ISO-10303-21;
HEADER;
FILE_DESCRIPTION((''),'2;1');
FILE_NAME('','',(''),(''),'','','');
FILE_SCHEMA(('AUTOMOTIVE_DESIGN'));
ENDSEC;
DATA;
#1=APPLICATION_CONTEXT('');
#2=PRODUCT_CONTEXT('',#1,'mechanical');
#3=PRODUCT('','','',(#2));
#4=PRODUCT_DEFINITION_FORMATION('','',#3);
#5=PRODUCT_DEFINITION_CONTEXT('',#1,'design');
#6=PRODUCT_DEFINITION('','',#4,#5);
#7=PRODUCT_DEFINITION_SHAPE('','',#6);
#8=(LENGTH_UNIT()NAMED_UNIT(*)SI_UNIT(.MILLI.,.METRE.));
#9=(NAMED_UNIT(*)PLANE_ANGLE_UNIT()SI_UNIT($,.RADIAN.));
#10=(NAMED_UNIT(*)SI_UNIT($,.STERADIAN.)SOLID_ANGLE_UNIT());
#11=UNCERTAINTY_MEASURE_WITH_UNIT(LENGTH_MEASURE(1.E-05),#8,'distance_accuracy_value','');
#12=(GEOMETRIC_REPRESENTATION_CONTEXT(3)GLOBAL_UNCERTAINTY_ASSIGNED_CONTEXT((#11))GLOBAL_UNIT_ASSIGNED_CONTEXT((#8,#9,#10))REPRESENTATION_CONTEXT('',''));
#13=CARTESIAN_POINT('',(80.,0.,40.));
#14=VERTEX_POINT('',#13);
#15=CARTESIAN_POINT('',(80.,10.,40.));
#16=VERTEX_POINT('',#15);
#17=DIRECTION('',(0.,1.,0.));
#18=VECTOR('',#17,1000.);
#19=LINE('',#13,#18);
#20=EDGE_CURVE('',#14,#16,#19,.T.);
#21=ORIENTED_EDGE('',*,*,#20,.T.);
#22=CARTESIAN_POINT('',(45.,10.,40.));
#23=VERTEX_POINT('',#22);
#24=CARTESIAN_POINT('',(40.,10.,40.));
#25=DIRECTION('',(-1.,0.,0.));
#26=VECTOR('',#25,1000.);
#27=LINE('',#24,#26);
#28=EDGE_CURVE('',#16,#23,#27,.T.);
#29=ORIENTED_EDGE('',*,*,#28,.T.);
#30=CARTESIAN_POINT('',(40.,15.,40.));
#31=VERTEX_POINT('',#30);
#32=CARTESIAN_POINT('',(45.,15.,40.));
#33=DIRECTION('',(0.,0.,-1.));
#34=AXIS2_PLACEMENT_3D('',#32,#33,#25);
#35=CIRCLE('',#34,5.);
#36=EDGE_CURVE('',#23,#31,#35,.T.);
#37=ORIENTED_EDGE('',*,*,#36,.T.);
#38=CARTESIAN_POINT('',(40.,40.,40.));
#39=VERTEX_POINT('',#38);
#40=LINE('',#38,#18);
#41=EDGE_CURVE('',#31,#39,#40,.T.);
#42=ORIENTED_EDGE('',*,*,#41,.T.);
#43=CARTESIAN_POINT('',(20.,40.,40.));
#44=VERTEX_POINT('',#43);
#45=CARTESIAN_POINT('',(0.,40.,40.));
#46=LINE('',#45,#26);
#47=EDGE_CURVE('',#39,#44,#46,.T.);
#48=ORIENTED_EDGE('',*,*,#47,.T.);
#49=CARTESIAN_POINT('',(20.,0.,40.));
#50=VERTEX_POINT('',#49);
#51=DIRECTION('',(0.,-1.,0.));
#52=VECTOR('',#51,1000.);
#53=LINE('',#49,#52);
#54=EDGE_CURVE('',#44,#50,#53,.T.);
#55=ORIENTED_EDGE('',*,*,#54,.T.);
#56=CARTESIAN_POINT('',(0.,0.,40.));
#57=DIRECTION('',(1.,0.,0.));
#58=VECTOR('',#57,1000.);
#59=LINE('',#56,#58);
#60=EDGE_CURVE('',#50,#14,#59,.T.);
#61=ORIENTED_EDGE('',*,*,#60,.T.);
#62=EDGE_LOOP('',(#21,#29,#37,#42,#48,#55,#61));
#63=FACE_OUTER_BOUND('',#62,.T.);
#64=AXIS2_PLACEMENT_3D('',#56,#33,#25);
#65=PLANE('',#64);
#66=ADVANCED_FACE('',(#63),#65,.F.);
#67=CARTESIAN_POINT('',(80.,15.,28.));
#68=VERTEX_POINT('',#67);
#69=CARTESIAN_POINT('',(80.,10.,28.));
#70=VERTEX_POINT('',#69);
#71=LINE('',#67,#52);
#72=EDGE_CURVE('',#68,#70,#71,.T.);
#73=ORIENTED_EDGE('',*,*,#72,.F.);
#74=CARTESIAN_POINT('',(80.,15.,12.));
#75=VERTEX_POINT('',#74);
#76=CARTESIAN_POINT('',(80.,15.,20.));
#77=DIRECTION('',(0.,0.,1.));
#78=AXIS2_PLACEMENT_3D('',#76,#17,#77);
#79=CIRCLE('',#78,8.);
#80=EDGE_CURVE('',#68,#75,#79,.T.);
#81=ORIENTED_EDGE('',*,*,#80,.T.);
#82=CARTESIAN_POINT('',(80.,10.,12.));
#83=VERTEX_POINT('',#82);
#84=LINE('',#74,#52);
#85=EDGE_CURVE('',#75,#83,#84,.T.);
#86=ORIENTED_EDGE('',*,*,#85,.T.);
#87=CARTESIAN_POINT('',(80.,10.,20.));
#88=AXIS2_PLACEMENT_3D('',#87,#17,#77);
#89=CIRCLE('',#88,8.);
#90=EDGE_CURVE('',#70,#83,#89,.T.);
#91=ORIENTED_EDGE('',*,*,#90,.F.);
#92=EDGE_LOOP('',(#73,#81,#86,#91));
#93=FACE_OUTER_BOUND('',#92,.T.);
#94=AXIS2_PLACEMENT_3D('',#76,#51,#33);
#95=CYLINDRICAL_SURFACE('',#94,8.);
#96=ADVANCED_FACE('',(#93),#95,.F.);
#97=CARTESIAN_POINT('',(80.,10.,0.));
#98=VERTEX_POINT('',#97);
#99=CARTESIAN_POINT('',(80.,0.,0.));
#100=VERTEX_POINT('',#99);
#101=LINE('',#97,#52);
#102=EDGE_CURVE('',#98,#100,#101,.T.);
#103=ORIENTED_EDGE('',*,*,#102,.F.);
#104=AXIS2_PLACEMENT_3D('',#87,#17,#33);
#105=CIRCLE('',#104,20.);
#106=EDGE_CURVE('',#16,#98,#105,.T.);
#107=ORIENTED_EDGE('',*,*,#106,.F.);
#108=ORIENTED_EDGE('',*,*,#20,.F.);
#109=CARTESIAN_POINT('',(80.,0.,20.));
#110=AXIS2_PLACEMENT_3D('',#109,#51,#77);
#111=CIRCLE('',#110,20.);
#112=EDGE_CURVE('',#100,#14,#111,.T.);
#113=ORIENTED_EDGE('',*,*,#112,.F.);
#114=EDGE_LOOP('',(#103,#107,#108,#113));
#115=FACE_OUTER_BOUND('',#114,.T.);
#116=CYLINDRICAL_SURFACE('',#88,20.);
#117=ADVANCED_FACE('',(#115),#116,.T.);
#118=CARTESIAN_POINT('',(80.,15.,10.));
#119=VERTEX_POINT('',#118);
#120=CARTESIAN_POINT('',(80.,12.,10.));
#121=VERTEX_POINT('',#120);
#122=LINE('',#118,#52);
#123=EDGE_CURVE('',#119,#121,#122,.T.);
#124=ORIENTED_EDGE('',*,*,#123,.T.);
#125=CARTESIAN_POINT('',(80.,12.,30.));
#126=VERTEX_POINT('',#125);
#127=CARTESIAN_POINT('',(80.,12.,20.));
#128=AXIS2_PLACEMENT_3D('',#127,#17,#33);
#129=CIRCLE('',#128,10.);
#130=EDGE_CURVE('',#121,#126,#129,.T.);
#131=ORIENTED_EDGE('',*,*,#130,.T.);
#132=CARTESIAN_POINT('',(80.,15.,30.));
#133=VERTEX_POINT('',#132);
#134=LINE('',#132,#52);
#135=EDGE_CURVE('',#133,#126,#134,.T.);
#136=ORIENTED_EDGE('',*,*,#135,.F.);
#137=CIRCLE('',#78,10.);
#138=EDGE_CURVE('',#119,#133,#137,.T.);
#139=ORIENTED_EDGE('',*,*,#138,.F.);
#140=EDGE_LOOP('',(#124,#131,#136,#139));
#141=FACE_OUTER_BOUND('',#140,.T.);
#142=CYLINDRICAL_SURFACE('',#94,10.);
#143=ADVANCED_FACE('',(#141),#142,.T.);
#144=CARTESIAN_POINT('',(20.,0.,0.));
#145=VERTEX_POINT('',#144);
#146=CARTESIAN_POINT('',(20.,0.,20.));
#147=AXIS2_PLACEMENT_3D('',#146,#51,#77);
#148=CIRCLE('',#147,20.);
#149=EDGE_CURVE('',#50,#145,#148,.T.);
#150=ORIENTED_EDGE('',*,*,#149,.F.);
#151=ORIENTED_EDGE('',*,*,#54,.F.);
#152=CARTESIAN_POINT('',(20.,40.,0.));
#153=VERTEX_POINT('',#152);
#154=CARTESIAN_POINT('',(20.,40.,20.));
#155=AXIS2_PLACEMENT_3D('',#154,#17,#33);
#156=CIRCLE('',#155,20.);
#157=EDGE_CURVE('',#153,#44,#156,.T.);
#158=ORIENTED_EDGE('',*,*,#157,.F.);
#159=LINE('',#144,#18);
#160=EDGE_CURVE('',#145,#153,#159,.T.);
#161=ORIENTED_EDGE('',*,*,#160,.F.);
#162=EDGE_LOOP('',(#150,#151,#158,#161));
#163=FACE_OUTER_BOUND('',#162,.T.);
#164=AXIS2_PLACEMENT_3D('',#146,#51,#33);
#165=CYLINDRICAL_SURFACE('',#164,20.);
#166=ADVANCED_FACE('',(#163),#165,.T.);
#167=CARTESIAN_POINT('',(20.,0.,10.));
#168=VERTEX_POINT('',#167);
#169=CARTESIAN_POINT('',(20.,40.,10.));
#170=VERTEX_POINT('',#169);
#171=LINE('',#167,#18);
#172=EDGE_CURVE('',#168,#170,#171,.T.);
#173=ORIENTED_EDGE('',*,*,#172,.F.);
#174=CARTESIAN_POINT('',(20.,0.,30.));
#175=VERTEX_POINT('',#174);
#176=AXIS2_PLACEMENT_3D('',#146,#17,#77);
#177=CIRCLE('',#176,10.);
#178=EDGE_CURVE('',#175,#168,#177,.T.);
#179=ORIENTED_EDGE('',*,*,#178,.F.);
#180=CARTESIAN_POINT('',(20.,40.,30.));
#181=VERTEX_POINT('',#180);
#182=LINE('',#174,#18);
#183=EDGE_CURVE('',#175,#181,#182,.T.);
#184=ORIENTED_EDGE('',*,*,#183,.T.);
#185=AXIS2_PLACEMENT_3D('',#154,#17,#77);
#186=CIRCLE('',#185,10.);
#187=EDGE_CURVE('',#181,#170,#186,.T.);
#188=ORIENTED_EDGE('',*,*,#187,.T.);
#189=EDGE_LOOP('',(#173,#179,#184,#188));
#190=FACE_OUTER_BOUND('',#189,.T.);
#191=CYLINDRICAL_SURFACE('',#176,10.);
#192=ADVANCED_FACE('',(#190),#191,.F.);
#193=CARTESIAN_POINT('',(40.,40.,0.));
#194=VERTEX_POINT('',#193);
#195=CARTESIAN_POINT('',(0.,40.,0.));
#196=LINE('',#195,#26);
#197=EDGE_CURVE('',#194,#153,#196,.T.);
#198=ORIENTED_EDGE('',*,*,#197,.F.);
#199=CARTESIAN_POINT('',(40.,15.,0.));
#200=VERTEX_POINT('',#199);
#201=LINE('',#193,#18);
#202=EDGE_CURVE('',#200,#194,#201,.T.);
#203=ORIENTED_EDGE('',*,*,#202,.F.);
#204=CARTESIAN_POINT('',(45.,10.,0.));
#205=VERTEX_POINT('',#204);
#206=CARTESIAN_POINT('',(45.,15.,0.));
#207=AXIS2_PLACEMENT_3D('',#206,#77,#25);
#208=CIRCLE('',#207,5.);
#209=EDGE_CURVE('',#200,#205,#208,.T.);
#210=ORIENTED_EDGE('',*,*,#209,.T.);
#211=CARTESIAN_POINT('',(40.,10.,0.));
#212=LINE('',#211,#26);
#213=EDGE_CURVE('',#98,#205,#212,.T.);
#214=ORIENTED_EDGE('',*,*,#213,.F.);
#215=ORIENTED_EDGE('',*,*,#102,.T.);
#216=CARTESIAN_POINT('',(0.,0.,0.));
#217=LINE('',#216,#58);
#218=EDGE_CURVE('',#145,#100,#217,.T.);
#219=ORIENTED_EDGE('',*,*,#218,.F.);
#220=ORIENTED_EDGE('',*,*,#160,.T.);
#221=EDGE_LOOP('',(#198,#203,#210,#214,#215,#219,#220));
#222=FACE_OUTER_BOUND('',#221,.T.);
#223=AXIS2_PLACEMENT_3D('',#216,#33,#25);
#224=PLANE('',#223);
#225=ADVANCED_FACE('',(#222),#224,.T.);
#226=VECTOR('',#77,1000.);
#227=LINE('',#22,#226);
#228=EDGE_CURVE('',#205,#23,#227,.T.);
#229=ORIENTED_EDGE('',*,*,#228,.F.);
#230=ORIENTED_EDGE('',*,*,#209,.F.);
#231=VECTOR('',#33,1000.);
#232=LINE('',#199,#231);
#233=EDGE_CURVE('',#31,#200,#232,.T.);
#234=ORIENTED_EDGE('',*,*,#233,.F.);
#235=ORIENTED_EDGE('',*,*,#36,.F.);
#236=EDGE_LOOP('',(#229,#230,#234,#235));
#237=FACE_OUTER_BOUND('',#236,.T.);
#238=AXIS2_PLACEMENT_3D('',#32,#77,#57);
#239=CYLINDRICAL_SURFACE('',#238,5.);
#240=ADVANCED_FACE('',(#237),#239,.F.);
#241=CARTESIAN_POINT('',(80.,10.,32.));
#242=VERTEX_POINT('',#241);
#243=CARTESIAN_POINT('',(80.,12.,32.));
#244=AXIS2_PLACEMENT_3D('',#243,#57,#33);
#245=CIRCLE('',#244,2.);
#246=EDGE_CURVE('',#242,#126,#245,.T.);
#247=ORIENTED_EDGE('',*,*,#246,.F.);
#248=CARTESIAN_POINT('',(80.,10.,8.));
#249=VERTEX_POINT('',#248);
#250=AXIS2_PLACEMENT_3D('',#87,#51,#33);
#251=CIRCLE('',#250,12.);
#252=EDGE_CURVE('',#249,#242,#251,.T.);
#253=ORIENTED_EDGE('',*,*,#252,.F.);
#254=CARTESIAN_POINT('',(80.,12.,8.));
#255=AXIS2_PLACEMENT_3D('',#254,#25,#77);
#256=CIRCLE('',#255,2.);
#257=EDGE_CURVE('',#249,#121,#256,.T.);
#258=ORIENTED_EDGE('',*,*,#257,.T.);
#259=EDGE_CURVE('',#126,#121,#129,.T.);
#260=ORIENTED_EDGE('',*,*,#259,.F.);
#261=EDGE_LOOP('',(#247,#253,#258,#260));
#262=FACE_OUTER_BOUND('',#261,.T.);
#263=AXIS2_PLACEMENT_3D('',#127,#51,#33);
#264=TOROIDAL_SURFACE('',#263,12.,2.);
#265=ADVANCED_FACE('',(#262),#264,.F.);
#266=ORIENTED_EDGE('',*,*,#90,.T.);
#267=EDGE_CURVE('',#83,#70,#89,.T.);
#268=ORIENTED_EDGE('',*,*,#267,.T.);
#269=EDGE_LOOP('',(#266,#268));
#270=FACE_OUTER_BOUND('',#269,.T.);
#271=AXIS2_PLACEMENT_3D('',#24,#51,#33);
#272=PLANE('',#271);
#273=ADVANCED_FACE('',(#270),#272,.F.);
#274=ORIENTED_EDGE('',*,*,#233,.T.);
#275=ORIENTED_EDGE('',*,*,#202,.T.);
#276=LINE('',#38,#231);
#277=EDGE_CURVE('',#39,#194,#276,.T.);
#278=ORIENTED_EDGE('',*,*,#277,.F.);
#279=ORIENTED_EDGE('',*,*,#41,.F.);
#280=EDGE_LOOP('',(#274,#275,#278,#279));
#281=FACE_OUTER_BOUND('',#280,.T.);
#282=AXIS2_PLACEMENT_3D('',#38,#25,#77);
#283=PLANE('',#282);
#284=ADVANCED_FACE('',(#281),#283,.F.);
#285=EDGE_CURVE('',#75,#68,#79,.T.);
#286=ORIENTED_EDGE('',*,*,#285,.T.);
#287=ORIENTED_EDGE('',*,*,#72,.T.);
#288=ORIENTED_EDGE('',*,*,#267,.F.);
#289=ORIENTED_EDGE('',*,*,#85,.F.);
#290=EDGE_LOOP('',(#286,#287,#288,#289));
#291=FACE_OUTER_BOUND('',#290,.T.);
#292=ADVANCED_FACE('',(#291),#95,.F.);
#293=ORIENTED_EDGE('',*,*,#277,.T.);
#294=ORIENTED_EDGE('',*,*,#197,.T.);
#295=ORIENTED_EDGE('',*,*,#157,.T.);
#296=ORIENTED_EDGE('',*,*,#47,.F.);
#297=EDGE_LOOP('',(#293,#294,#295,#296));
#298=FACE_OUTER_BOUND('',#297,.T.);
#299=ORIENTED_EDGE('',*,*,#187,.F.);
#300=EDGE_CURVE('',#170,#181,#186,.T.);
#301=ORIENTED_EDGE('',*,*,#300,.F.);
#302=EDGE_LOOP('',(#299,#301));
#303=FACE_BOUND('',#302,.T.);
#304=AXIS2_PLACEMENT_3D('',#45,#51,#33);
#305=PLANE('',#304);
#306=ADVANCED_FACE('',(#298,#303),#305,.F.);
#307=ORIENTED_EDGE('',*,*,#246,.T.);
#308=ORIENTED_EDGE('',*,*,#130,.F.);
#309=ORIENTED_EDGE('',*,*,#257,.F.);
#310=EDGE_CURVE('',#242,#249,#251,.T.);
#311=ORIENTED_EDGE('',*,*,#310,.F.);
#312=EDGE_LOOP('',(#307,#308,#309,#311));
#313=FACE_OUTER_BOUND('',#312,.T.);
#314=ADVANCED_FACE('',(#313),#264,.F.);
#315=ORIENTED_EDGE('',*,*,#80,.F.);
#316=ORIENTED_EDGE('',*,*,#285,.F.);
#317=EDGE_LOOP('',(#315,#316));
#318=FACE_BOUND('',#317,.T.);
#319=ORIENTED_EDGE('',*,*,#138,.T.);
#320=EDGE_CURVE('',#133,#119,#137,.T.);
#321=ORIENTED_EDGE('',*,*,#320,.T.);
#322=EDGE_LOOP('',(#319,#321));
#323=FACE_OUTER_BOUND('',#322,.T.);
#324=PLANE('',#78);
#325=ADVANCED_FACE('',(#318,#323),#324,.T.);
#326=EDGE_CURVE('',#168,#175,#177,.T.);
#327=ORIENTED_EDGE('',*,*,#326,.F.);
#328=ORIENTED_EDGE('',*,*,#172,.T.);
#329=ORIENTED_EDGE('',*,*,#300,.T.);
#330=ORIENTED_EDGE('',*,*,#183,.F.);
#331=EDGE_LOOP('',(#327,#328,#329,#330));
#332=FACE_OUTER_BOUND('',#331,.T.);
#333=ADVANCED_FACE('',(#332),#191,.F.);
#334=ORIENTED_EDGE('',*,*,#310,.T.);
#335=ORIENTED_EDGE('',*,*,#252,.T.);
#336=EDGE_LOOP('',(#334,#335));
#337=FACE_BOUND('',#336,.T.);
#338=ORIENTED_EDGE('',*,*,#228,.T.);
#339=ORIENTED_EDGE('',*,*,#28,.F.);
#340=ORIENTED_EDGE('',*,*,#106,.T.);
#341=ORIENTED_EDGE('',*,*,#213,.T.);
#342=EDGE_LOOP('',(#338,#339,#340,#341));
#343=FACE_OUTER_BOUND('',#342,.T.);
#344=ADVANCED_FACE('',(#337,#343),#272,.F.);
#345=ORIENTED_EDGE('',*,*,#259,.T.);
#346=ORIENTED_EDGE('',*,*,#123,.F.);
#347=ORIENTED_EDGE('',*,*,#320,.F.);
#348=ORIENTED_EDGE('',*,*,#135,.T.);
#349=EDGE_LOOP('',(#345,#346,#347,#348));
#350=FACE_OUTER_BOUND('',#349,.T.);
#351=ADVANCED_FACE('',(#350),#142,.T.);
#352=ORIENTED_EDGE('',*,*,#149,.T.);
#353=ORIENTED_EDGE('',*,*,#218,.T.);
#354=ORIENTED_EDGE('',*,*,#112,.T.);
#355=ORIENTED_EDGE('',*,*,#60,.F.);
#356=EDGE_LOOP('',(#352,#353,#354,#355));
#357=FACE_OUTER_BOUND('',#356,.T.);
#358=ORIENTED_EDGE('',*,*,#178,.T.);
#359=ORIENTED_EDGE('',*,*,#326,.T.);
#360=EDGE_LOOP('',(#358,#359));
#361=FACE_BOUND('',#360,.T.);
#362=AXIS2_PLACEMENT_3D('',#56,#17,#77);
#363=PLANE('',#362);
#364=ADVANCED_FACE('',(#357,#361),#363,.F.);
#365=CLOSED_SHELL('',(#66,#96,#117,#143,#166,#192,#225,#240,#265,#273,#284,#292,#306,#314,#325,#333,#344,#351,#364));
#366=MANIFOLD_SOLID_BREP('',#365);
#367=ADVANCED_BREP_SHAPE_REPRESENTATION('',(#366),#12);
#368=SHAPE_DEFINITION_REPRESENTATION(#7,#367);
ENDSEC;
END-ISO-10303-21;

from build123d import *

# Parameters (mm, degrees)
L_BODY_DEPTH               = 40
LUG_END_ROUND_RADIUS       = 20
LUG_END_ROUND_LENGTH       = 40
LUG_BORE_SKETCH_R          = 10
LUG_BORE_20_DEPTH          = 40
BASE_END_ROUND_RADIUS      = 20
BASE_END_ROUND_LENGTH      = 10
RING_BOSS_SKETCH_R         = 10
RING_BOSS_SKETCH_R_2       = 8
RING_BOSS_20X_16_DEPTH     = 5
INNER_CORNER_FILLET_R5_R   = 5
RING_BOSS_BASE_FILLET_R2_R = 2


with BuildPart() as part:
    # L Profile Sketch → L Body (new body)
    with BuildSketch(Plane.XY):
        Polygon((0, 0), (100, 0), (100, 10), (40, 10), (40, 40), (0, 40), align=None)
    extrude(amount=L_BODY_DEPTH)

    # Lug End Round: full round fillet: the end face becomes a half cylinder, R = half its width
    lug_end_round_face = Plane((0, 20, 20), x_dir=(0, 1, 0), z_dir=(-1, 0, 0))  # on the end face: x along it, z out of the body
    lug_end_round_slab = lug_end_round_face.offset(-LUG_END_ROUND_RADIUS / 2) * Box(LUG_END_ROUND_LENGTH, 2 * LUG_END_ROUND_RADIUS, LUG_END_ROUND_RADIUS, mode=Mode.PRIVATE)  # the body's end, R deep
    lug_end_round_round = Plane((20, 20, 20), x_dir=(-1, 0, 0), z_dir=(0, 1, 0)) * Cylinder(LUG_END_ROUND_RADIUS, LUG_END_ROUND_LENGTH, mode=Mode.PRIVATE)  # its axis R under the face
    add(lug_end_round_slab - lug_end_round_round, mode=Mode.SUBTRACT)

    # Lug Bore Sketch → Lug Bore _20 (cut)
    with BuildSketch(Plane(origin=(0, 40, 0), x_dir=(1, 0, 0), z_dir=(0, 1, 0))):
        with Locations(Location((20, -20, 0), (0, 0, 270))):
            Circle(LUG_BORE_SKETCH_R)
    extrude(amount=-LUG_BORE_20_DEPTH, mode=Mode.SUBTRACT)

    # Base End Round: full round fillet: the end face becomes a half cylinder, R = half its width
    base_end_round_face = Plane((100, 5, 20), x_dir=(0, -1, 0), z_dir=(1, 0, 0))  # on the end face: x along it, z out of the body
    base_end_round_slab = base_end_round_face.offset(-BASE_END_ROUND_RADIUS / 2) * Box(BASE_END_ROUND_LENGTH, 2 * BASE_END_ROUND_RADIUS, BASE_END_ROUND_RADIUS, mode=Mode.PRIVATE)  # the body's end, R deep
    base_end_round_round = Plane((80, 5, 20), x_dir=(1, 0, 0), z_dir=(0, -1, 0)) * Cylinder(BASE_END_ROUND_RADIUS, BASE_END_ROUND_LENGTH, mode=Mode.PRIVATE)  # its axis R under the face
    add(base_end_round_slab - base_end_round_round, mode=Mode.SUBTRACT)

    # Ring Boss Sketch → Ring Boss _20x_16 (add)
    with BuildSketch(Plane(origin=(0, 10, 0), x_dir=(1, 0, 0), z_dir=(0, 1, 0))):
        with Locations(Location((80, -20, 0), (0, 0, 90))):
            Circle(RING_BOSS_SKETCH_R)
        with Locations(Location((80, -20, 0), (0, 0, 270))):
            Circle(RING_BOSS_SKETCH_R_2, mode=Mode.SUBTRACT)
    extrude(amount=RING_BOSS_20X_16_DEPTH)

    # Inner Corner Fillet R5
    inner_corner_fillet_r5_edges = [part.edges().sort_by_distance(p)[0] for p in [
        (40, 10, 20),
    ]]
    fillet(inner_corner_fillet_r5_edges, radius=INNER_CORNER_FILLET_R5_R)

    # Ring Boss Base Fillet R2
    ring_boss_base_fillet_r2_edges = [part.edges().sort_by_distance(p)[0] for p in [
        (80, 10, 30),
    ]]
    fillet(ring_boss_base_fillet_r2_edges, radius=RING_BOSS_BASE_FILLET_R2_R)


solid = part.part
